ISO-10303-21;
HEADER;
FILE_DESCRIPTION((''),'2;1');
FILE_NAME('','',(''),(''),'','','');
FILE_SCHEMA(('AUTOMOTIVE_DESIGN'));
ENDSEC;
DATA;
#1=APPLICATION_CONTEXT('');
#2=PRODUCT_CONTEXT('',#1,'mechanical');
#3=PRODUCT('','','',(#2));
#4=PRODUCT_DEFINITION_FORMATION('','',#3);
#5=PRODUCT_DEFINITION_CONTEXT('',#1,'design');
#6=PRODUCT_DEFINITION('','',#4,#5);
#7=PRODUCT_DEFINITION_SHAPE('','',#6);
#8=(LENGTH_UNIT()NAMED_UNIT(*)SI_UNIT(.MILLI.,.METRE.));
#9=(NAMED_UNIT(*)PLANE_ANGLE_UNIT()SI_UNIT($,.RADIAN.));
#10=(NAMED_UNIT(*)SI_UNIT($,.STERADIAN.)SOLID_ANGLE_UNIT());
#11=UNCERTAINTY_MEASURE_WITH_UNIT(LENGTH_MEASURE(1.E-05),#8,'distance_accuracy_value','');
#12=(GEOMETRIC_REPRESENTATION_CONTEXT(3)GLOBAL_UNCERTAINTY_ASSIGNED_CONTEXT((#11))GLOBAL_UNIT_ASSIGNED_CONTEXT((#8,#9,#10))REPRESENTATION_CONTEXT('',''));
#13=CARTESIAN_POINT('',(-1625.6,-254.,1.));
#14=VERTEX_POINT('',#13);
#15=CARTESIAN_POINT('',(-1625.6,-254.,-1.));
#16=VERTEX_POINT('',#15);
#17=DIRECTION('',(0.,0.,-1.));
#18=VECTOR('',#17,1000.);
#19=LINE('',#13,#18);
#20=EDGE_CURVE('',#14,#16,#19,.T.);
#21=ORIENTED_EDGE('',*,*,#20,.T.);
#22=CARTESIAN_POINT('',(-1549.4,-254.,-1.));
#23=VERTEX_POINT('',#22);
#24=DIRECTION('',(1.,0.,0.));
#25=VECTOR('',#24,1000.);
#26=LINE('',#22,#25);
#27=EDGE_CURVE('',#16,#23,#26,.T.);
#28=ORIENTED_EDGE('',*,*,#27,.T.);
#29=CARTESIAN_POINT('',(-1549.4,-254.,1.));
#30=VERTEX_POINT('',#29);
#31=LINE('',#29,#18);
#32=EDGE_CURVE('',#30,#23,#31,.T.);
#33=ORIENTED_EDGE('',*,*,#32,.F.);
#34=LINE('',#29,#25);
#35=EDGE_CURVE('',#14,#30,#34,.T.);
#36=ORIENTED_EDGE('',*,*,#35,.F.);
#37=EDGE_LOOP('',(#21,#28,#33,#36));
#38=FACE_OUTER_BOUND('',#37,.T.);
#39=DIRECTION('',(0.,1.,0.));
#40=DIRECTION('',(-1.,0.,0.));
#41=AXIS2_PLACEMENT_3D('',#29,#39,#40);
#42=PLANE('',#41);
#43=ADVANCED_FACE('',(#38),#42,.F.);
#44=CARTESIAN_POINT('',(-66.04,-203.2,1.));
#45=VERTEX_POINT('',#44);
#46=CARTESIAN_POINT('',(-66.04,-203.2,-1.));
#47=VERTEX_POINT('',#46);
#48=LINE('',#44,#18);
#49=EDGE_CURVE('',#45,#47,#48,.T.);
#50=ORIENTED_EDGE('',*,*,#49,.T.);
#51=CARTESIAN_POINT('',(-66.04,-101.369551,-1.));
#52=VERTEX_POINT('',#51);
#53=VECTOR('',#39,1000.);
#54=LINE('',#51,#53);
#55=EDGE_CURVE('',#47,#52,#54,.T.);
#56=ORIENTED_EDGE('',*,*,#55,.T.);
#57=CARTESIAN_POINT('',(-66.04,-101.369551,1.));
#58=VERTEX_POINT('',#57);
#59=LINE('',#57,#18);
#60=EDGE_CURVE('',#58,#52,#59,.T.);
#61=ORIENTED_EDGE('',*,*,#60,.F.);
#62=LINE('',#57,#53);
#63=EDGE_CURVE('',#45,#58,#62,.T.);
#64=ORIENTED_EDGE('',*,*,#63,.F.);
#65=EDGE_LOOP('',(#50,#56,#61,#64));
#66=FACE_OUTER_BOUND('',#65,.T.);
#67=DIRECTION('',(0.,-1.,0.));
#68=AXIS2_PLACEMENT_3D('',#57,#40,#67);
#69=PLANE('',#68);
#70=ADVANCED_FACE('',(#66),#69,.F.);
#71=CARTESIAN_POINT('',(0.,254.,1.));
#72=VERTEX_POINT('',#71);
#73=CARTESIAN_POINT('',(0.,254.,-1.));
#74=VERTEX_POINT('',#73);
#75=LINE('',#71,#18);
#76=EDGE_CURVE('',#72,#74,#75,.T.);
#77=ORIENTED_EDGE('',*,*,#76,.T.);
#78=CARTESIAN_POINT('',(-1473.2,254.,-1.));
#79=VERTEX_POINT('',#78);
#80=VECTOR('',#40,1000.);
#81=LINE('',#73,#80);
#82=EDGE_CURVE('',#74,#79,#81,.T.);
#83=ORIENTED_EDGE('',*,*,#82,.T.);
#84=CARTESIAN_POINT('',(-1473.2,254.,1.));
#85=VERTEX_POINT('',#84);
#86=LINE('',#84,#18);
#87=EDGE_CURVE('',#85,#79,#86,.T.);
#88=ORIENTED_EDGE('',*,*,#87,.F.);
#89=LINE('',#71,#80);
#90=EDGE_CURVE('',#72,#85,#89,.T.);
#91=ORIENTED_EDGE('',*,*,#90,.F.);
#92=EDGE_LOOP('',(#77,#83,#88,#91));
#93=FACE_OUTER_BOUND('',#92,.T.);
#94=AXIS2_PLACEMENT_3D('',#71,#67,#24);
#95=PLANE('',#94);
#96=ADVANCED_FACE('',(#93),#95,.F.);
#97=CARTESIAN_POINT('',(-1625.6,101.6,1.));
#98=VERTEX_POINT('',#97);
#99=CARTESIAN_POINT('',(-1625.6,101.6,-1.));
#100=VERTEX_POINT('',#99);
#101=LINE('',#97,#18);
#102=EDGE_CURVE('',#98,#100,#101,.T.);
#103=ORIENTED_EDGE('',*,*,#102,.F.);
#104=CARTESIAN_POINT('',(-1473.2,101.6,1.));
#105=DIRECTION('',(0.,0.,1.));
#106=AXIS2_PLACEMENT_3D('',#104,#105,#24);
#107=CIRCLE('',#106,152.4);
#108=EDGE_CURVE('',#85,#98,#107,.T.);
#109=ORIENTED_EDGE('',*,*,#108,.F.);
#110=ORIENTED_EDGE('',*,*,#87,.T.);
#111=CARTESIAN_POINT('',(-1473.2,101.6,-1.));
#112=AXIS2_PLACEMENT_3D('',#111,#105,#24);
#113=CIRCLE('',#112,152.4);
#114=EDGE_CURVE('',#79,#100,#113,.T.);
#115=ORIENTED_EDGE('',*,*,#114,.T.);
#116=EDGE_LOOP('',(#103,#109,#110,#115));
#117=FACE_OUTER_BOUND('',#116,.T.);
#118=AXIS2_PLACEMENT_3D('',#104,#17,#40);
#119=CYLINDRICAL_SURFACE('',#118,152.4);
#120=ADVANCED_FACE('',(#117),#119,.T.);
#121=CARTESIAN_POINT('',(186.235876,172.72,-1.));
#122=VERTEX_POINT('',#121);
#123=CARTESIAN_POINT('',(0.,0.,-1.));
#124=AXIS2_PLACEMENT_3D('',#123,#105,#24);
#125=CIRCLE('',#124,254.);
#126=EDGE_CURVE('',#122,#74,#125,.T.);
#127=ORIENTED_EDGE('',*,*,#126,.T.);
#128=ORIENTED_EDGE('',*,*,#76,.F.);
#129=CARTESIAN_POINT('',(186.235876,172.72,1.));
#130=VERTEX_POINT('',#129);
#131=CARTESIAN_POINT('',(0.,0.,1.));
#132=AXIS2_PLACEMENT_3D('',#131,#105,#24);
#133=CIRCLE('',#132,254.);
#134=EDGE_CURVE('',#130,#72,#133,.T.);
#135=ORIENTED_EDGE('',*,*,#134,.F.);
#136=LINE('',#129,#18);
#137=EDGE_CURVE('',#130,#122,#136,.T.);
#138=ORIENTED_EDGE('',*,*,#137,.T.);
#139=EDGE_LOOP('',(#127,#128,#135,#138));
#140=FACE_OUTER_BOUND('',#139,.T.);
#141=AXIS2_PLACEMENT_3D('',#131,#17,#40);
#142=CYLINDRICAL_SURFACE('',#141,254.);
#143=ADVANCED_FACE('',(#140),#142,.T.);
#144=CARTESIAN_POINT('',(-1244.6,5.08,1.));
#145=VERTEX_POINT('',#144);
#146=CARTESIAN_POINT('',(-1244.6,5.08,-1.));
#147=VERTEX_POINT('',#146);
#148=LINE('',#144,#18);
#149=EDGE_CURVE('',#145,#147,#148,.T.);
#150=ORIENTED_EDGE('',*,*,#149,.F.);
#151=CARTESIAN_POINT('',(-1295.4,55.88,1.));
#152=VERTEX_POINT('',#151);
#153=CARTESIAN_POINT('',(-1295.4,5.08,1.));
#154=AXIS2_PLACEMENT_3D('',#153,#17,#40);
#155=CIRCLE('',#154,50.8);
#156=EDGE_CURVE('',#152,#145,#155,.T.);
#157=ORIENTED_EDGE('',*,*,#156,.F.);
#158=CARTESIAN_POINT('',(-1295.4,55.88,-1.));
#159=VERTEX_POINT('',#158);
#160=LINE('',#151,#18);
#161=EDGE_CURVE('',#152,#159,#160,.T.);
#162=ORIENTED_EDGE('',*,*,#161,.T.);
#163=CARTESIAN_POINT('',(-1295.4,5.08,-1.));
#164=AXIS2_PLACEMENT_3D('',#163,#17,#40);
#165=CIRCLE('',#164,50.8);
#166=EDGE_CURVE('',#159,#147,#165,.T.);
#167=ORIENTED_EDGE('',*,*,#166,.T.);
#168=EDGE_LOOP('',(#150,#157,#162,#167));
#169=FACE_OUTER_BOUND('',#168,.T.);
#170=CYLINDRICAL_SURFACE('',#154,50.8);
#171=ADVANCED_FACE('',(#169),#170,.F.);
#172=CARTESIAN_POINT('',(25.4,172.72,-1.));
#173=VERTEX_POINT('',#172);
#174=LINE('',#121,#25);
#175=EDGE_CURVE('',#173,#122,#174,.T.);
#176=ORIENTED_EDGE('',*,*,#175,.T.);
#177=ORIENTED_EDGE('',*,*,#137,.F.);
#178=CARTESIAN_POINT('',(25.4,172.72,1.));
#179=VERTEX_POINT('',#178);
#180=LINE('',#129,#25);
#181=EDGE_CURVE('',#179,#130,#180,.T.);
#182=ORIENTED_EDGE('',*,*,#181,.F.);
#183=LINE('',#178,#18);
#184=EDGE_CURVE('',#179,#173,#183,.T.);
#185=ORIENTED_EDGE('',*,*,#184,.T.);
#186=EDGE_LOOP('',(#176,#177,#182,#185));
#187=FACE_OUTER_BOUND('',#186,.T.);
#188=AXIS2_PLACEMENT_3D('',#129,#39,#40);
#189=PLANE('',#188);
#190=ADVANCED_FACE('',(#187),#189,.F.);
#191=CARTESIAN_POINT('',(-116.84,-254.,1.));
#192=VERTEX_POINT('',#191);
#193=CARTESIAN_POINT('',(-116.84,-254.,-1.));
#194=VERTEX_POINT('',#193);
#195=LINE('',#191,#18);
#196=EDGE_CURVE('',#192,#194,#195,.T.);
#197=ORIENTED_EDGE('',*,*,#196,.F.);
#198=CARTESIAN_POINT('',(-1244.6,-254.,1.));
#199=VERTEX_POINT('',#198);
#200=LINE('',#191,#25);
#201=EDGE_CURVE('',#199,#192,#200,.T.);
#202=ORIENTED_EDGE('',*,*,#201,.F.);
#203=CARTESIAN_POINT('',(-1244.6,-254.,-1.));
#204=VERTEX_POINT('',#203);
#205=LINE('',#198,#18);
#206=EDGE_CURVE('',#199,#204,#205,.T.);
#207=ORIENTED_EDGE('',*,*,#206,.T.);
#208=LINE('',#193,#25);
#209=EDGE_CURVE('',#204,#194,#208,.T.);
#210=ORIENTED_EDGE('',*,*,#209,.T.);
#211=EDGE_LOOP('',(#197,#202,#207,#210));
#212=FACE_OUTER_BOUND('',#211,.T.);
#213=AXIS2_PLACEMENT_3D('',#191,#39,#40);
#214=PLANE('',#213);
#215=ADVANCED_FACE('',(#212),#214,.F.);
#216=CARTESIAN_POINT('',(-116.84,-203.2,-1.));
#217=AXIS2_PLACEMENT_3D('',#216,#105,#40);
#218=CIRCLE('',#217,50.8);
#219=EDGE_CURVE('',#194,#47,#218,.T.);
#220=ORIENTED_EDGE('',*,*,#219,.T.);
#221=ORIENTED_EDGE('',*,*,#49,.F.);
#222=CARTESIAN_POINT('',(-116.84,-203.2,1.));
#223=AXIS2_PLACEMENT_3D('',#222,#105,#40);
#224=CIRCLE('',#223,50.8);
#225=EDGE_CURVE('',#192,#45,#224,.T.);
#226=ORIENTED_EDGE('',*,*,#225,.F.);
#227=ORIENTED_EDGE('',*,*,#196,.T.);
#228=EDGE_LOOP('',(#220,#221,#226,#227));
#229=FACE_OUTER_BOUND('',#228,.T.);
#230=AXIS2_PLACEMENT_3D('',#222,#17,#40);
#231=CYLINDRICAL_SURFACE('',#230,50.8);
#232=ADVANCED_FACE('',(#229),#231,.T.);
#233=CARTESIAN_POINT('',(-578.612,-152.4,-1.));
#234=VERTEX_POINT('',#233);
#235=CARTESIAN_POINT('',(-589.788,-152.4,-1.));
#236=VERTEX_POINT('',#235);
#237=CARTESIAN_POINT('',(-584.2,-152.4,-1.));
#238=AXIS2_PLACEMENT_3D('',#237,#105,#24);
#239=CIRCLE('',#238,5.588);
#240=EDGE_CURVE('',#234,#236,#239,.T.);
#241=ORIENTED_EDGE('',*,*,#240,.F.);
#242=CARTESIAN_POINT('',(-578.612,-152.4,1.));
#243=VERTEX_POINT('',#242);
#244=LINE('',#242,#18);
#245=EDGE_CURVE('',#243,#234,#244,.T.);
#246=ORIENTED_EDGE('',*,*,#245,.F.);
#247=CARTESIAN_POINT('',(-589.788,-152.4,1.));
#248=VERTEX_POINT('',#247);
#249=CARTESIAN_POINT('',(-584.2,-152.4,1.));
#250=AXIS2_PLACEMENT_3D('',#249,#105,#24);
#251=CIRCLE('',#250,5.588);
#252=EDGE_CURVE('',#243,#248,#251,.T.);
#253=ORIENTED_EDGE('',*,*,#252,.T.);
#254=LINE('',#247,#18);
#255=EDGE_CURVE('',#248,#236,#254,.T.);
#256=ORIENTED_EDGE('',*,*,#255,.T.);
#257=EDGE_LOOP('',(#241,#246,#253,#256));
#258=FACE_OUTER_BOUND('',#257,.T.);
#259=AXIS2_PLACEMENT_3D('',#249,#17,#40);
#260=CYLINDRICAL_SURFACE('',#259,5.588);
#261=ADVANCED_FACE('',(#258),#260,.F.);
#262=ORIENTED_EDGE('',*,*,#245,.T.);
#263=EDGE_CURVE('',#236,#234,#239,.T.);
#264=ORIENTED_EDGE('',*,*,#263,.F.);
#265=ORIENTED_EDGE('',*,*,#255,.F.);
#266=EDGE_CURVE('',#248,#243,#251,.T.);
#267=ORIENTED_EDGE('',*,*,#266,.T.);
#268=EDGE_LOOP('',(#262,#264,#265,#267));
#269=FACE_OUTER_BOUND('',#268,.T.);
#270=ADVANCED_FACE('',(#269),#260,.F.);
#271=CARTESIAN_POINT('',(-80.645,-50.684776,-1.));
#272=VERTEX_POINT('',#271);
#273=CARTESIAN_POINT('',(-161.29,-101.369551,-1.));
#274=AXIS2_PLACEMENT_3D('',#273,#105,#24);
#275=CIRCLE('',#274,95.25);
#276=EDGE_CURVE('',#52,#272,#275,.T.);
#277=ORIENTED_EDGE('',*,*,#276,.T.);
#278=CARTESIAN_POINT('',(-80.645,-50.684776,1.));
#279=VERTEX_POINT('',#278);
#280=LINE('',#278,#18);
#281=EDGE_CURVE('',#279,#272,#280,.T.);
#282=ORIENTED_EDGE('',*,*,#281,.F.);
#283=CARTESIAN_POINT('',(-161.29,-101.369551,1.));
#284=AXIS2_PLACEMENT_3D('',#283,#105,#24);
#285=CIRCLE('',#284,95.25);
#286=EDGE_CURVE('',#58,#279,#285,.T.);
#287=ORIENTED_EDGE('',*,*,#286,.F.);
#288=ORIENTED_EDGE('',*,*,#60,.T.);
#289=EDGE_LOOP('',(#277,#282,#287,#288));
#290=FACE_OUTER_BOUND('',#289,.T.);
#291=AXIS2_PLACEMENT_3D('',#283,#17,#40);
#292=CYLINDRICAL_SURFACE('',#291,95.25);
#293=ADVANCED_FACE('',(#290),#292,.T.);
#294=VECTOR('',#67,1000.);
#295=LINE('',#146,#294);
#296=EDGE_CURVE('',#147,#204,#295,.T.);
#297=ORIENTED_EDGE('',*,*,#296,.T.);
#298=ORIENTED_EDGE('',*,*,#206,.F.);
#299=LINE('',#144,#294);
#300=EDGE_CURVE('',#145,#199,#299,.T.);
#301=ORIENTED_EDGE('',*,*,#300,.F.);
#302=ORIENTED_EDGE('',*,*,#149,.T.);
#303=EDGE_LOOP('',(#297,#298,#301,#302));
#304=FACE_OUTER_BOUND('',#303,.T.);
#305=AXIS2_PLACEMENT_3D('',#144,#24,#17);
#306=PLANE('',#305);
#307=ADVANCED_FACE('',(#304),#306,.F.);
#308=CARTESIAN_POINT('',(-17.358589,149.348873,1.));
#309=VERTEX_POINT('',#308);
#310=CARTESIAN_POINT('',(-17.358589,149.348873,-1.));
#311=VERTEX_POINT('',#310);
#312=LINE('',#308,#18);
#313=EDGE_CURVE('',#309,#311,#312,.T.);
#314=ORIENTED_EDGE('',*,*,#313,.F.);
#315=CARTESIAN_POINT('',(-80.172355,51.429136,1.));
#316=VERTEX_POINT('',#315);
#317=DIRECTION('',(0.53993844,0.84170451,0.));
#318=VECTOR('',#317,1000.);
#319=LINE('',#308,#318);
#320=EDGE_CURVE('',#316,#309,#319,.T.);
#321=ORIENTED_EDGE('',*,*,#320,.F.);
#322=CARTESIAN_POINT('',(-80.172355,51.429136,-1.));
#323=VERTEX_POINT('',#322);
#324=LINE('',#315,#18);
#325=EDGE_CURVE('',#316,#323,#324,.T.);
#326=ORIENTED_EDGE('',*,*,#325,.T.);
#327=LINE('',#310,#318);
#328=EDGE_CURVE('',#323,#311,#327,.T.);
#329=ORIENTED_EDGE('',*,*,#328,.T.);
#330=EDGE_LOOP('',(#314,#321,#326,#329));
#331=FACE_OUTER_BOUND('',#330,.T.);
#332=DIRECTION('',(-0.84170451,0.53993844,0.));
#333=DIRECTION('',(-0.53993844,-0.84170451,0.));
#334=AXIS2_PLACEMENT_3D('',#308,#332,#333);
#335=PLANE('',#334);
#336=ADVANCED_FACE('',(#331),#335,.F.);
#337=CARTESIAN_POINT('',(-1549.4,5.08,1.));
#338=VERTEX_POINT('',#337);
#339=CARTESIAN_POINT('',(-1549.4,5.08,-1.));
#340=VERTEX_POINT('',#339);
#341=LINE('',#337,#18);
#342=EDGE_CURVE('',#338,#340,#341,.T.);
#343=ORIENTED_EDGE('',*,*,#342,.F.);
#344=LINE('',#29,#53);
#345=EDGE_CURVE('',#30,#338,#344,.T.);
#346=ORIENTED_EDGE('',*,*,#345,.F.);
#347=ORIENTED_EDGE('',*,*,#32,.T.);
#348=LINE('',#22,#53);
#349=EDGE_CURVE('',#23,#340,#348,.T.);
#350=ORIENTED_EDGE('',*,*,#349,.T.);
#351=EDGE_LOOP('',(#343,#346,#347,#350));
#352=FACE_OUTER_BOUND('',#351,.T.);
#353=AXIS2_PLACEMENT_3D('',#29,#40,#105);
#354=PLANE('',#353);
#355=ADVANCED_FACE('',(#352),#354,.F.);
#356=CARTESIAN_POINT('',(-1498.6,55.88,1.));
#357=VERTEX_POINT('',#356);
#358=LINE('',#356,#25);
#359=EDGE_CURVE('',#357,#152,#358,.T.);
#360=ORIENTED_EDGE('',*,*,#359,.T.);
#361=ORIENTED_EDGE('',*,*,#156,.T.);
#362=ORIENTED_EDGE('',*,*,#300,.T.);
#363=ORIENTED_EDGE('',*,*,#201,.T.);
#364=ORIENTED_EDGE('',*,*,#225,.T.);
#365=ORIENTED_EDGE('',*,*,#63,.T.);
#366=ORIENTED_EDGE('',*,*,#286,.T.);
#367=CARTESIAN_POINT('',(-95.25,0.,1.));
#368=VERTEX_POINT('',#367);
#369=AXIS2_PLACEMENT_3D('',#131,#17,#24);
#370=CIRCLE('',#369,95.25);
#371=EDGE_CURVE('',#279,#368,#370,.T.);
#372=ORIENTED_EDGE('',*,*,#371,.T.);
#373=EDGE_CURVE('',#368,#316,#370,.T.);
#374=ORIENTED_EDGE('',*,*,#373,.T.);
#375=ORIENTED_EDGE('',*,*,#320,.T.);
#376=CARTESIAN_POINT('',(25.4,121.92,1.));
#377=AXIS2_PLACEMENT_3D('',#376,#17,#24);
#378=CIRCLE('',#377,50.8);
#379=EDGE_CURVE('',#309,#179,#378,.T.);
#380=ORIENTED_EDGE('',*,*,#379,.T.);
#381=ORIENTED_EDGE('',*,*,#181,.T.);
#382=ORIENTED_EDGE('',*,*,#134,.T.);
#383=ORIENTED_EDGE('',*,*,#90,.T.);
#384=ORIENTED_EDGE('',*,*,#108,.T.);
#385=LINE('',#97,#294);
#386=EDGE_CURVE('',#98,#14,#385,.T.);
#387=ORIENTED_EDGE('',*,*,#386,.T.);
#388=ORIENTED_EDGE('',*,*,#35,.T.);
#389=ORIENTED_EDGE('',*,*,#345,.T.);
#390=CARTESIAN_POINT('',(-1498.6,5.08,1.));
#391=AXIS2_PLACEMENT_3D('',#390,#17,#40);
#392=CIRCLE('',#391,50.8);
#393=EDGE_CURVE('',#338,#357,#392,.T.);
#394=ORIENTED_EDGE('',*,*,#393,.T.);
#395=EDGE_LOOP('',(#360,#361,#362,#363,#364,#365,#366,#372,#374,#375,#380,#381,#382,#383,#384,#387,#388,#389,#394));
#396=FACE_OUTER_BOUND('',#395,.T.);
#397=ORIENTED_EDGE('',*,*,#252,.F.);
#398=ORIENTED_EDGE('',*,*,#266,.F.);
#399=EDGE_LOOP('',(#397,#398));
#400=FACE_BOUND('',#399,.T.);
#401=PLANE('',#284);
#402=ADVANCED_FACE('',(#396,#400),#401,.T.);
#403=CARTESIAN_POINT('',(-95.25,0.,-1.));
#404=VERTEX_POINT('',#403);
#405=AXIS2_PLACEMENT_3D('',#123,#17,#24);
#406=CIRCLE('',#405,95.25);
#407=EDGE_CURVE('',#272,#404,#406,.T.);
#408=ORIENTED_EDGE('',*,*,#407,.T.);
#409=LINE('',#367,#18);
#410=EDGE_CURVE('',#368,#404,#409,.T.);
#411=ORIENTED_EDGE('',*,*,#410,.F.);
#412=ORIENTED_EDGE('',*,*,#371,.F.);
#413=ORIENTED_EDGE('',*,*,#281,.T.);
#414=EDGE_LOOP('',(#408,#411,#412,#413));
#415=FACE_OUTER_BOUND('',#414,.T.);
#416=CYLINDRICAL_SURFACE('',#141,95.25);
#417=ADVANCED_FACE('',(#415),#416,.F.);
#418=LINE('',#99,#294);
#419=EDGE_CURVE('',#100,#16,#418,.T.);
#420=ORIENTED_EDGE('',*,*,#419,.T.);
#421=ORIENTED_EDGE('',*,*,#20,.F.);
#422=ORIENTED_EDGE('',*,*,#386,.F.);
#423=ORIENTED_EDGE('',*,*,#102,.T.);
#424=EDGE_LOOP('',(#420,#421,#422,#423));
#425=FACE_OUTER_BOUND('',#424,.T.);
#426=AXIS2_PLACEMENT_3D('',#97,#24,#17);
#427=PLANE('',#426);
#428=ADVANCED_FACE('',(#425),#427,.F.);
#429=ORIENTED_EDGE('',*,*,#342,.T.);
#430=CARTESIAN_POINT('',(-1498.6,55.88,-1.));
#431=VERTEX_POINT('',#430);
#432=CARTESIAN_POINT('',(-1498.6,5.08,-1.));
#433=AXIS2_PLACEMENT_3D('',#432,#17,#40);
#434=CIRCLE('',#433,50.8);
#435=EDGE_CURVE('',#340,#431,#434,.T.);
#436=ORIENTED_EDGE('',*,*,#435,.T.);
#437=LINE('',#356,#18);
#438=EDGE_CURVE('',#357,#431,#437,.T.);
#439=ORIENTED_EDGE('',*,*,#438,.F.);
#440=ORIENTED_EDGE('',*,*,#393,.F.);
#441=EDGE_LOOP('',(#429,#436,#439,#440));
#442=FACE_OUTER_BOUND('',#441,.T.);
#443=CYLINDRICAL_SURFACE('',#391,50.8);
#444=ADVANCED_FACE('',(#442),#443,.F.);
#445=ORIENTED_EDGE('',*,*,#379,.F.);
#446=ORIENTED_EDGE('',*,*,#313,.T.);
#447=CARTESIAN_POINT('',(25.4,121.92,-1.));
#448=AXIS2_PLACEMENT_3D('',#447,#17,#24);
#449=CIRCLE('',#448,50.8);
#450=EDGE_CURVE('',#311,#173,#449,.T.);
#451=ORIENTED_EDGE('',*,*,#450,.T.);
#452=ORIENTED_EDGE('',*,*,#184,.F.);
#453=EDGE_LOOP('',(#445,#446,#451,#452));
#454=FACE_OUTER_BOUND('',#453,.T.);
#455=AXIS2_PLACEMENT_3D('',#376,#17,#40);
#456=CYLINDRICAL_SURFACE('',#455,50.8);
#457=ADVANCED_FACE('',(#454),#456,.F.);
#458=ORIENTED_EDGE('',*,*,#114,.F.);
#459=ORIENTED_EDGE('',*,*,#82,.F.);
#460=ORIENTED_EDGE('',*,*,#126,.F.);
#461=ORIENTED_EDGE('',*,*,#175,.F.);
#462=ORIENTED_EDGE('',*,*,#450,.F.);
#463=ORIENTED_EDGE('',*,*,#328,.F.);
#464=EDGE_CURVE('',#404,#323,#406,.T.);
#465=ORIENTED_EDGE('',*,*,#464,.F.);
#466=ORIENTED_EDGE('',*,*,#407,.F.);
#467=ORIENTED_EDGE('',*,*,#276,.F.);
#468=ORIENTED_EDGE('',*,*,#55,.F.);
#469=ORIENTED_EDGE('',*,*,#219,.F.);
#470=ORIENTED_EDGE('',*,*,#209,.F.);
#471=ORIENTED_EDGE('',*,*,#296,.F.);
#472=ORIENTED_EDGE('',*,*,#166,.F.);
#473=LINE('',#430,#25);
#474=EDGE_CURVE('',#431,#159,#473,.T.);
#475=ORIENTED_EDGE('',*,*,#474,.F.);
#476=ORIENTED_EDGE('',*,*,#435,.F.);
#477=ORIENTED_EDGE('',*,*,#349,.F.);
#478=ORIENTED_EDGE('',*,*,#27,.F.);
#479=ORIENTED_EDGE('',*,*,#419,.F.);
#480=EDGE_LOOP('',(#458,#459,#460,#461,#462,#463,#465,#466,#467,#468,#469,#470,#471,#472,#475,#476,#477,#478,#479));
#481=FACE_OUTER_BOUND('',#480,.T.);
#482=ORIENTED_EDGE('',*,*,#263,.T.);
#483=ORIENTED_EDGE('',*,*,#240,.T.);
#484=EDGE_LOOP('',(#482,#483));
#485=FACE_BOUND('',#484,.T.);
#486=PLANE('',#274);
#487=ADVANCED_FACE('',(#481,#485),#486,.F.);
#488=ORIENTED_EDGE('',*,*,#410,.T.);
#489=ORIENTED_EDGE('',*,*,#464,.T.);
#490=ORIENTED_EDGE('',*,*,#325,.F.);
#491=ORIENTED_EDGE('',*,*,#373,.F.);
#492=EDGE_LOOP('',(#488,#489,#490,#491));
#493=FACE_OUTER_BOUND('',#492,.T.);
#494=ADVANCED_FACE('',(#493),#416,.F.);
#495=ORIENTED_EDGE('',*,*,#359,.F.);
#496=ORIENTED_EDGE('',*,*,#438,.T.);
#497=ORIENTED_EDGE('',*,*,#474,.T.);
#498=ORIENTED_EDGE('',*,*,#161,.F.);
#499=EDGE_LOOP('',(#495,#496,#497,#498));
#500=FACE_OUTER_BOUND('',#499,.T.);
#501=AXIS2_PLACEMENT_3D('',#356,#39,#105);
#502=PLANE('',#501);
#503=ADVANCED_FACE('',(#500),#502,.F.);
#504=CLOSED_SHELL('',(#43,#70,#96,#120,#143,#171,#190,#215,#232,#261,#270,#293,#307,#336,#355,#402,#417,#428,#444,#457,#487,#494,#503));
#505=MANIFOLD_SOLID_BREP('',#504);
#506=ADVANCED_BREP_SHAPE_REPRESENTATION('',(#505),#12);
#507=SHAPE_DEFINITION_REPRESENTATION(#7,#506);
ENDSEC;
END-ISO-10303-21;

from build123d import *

# Parameters (mm, degrees)
SKETCH1_R           = 5.588
BOSS_EXTRUDE1_DEPTH = 1


with BuildPart() as part:
    # Sketch1 → Boss-Extrude1 (new, symmetric)
    with BuildSketch(Plane.XY):
        with BuildLine():
            Line((186.235876243, 172.72), (25.4, 172.72))
            ThreePointArc((25.4, 172.72), (1.035545712, 166.495928114), (-17.35858909, 149.348872727))
            Line((-17.35858909, 149.348872727), (-80.172354543, 51.429136363))
            ThreePointArc((-80.172354543, 51.429136363), (-95.248979697, 0.440870364), (-80.645, -50.684775574))
            ThreePointArc((-80.645, -50.684775574), (-69.764050811, -74.996020383), (-66.04, -101.369551148))
            Line((-66.04, -101.369551148), (-66.04, -203.2))
            ThreePointArc((-66.04, -203.2), (-80.918975516, -239.121024484), (-116.84, -254))
            Line((-116.84, -254), (-1244.6, -254))
            Line((-1244.6, -254), (-1244.6, 5.08))
            ThreePointArc((-1244.6, 5.08), (-1259.478975516, 41.001024484), (-1295.4, 55.88))
            Line((-1295.4, 55.88), (-1498.6, 55.88))
            ThreePointArc((-1498.6, 55.88), (-1534.521024484, 41.001024484), (-1549.4, 5.08))
            Line((-1549.4, 5.08), (-1549.4, -254))
            Line((-1549.4, -254), (-1625.6, -254))
            Line((-1625.6, -254), (-1625.6, 101.6))
            ThreePointArc((-1625.6, 101.6), (-1580.963073453, 209.363073453), (-1473.2, 254))
            Line((-1473.2, 254), (0, 254))
            ThreePointArc((0, 254), (101.6, 232.794845304), (186.235876243, 172.72))
        make_face()
        with Locations((-584.2, -152.4)):
            Circle(SKETCH1_R, mode=Mode.SUBTRACT)
    extrude(amount=BOSS_EXTRUDE1_DEPTH, both=True)


solid = part.part
